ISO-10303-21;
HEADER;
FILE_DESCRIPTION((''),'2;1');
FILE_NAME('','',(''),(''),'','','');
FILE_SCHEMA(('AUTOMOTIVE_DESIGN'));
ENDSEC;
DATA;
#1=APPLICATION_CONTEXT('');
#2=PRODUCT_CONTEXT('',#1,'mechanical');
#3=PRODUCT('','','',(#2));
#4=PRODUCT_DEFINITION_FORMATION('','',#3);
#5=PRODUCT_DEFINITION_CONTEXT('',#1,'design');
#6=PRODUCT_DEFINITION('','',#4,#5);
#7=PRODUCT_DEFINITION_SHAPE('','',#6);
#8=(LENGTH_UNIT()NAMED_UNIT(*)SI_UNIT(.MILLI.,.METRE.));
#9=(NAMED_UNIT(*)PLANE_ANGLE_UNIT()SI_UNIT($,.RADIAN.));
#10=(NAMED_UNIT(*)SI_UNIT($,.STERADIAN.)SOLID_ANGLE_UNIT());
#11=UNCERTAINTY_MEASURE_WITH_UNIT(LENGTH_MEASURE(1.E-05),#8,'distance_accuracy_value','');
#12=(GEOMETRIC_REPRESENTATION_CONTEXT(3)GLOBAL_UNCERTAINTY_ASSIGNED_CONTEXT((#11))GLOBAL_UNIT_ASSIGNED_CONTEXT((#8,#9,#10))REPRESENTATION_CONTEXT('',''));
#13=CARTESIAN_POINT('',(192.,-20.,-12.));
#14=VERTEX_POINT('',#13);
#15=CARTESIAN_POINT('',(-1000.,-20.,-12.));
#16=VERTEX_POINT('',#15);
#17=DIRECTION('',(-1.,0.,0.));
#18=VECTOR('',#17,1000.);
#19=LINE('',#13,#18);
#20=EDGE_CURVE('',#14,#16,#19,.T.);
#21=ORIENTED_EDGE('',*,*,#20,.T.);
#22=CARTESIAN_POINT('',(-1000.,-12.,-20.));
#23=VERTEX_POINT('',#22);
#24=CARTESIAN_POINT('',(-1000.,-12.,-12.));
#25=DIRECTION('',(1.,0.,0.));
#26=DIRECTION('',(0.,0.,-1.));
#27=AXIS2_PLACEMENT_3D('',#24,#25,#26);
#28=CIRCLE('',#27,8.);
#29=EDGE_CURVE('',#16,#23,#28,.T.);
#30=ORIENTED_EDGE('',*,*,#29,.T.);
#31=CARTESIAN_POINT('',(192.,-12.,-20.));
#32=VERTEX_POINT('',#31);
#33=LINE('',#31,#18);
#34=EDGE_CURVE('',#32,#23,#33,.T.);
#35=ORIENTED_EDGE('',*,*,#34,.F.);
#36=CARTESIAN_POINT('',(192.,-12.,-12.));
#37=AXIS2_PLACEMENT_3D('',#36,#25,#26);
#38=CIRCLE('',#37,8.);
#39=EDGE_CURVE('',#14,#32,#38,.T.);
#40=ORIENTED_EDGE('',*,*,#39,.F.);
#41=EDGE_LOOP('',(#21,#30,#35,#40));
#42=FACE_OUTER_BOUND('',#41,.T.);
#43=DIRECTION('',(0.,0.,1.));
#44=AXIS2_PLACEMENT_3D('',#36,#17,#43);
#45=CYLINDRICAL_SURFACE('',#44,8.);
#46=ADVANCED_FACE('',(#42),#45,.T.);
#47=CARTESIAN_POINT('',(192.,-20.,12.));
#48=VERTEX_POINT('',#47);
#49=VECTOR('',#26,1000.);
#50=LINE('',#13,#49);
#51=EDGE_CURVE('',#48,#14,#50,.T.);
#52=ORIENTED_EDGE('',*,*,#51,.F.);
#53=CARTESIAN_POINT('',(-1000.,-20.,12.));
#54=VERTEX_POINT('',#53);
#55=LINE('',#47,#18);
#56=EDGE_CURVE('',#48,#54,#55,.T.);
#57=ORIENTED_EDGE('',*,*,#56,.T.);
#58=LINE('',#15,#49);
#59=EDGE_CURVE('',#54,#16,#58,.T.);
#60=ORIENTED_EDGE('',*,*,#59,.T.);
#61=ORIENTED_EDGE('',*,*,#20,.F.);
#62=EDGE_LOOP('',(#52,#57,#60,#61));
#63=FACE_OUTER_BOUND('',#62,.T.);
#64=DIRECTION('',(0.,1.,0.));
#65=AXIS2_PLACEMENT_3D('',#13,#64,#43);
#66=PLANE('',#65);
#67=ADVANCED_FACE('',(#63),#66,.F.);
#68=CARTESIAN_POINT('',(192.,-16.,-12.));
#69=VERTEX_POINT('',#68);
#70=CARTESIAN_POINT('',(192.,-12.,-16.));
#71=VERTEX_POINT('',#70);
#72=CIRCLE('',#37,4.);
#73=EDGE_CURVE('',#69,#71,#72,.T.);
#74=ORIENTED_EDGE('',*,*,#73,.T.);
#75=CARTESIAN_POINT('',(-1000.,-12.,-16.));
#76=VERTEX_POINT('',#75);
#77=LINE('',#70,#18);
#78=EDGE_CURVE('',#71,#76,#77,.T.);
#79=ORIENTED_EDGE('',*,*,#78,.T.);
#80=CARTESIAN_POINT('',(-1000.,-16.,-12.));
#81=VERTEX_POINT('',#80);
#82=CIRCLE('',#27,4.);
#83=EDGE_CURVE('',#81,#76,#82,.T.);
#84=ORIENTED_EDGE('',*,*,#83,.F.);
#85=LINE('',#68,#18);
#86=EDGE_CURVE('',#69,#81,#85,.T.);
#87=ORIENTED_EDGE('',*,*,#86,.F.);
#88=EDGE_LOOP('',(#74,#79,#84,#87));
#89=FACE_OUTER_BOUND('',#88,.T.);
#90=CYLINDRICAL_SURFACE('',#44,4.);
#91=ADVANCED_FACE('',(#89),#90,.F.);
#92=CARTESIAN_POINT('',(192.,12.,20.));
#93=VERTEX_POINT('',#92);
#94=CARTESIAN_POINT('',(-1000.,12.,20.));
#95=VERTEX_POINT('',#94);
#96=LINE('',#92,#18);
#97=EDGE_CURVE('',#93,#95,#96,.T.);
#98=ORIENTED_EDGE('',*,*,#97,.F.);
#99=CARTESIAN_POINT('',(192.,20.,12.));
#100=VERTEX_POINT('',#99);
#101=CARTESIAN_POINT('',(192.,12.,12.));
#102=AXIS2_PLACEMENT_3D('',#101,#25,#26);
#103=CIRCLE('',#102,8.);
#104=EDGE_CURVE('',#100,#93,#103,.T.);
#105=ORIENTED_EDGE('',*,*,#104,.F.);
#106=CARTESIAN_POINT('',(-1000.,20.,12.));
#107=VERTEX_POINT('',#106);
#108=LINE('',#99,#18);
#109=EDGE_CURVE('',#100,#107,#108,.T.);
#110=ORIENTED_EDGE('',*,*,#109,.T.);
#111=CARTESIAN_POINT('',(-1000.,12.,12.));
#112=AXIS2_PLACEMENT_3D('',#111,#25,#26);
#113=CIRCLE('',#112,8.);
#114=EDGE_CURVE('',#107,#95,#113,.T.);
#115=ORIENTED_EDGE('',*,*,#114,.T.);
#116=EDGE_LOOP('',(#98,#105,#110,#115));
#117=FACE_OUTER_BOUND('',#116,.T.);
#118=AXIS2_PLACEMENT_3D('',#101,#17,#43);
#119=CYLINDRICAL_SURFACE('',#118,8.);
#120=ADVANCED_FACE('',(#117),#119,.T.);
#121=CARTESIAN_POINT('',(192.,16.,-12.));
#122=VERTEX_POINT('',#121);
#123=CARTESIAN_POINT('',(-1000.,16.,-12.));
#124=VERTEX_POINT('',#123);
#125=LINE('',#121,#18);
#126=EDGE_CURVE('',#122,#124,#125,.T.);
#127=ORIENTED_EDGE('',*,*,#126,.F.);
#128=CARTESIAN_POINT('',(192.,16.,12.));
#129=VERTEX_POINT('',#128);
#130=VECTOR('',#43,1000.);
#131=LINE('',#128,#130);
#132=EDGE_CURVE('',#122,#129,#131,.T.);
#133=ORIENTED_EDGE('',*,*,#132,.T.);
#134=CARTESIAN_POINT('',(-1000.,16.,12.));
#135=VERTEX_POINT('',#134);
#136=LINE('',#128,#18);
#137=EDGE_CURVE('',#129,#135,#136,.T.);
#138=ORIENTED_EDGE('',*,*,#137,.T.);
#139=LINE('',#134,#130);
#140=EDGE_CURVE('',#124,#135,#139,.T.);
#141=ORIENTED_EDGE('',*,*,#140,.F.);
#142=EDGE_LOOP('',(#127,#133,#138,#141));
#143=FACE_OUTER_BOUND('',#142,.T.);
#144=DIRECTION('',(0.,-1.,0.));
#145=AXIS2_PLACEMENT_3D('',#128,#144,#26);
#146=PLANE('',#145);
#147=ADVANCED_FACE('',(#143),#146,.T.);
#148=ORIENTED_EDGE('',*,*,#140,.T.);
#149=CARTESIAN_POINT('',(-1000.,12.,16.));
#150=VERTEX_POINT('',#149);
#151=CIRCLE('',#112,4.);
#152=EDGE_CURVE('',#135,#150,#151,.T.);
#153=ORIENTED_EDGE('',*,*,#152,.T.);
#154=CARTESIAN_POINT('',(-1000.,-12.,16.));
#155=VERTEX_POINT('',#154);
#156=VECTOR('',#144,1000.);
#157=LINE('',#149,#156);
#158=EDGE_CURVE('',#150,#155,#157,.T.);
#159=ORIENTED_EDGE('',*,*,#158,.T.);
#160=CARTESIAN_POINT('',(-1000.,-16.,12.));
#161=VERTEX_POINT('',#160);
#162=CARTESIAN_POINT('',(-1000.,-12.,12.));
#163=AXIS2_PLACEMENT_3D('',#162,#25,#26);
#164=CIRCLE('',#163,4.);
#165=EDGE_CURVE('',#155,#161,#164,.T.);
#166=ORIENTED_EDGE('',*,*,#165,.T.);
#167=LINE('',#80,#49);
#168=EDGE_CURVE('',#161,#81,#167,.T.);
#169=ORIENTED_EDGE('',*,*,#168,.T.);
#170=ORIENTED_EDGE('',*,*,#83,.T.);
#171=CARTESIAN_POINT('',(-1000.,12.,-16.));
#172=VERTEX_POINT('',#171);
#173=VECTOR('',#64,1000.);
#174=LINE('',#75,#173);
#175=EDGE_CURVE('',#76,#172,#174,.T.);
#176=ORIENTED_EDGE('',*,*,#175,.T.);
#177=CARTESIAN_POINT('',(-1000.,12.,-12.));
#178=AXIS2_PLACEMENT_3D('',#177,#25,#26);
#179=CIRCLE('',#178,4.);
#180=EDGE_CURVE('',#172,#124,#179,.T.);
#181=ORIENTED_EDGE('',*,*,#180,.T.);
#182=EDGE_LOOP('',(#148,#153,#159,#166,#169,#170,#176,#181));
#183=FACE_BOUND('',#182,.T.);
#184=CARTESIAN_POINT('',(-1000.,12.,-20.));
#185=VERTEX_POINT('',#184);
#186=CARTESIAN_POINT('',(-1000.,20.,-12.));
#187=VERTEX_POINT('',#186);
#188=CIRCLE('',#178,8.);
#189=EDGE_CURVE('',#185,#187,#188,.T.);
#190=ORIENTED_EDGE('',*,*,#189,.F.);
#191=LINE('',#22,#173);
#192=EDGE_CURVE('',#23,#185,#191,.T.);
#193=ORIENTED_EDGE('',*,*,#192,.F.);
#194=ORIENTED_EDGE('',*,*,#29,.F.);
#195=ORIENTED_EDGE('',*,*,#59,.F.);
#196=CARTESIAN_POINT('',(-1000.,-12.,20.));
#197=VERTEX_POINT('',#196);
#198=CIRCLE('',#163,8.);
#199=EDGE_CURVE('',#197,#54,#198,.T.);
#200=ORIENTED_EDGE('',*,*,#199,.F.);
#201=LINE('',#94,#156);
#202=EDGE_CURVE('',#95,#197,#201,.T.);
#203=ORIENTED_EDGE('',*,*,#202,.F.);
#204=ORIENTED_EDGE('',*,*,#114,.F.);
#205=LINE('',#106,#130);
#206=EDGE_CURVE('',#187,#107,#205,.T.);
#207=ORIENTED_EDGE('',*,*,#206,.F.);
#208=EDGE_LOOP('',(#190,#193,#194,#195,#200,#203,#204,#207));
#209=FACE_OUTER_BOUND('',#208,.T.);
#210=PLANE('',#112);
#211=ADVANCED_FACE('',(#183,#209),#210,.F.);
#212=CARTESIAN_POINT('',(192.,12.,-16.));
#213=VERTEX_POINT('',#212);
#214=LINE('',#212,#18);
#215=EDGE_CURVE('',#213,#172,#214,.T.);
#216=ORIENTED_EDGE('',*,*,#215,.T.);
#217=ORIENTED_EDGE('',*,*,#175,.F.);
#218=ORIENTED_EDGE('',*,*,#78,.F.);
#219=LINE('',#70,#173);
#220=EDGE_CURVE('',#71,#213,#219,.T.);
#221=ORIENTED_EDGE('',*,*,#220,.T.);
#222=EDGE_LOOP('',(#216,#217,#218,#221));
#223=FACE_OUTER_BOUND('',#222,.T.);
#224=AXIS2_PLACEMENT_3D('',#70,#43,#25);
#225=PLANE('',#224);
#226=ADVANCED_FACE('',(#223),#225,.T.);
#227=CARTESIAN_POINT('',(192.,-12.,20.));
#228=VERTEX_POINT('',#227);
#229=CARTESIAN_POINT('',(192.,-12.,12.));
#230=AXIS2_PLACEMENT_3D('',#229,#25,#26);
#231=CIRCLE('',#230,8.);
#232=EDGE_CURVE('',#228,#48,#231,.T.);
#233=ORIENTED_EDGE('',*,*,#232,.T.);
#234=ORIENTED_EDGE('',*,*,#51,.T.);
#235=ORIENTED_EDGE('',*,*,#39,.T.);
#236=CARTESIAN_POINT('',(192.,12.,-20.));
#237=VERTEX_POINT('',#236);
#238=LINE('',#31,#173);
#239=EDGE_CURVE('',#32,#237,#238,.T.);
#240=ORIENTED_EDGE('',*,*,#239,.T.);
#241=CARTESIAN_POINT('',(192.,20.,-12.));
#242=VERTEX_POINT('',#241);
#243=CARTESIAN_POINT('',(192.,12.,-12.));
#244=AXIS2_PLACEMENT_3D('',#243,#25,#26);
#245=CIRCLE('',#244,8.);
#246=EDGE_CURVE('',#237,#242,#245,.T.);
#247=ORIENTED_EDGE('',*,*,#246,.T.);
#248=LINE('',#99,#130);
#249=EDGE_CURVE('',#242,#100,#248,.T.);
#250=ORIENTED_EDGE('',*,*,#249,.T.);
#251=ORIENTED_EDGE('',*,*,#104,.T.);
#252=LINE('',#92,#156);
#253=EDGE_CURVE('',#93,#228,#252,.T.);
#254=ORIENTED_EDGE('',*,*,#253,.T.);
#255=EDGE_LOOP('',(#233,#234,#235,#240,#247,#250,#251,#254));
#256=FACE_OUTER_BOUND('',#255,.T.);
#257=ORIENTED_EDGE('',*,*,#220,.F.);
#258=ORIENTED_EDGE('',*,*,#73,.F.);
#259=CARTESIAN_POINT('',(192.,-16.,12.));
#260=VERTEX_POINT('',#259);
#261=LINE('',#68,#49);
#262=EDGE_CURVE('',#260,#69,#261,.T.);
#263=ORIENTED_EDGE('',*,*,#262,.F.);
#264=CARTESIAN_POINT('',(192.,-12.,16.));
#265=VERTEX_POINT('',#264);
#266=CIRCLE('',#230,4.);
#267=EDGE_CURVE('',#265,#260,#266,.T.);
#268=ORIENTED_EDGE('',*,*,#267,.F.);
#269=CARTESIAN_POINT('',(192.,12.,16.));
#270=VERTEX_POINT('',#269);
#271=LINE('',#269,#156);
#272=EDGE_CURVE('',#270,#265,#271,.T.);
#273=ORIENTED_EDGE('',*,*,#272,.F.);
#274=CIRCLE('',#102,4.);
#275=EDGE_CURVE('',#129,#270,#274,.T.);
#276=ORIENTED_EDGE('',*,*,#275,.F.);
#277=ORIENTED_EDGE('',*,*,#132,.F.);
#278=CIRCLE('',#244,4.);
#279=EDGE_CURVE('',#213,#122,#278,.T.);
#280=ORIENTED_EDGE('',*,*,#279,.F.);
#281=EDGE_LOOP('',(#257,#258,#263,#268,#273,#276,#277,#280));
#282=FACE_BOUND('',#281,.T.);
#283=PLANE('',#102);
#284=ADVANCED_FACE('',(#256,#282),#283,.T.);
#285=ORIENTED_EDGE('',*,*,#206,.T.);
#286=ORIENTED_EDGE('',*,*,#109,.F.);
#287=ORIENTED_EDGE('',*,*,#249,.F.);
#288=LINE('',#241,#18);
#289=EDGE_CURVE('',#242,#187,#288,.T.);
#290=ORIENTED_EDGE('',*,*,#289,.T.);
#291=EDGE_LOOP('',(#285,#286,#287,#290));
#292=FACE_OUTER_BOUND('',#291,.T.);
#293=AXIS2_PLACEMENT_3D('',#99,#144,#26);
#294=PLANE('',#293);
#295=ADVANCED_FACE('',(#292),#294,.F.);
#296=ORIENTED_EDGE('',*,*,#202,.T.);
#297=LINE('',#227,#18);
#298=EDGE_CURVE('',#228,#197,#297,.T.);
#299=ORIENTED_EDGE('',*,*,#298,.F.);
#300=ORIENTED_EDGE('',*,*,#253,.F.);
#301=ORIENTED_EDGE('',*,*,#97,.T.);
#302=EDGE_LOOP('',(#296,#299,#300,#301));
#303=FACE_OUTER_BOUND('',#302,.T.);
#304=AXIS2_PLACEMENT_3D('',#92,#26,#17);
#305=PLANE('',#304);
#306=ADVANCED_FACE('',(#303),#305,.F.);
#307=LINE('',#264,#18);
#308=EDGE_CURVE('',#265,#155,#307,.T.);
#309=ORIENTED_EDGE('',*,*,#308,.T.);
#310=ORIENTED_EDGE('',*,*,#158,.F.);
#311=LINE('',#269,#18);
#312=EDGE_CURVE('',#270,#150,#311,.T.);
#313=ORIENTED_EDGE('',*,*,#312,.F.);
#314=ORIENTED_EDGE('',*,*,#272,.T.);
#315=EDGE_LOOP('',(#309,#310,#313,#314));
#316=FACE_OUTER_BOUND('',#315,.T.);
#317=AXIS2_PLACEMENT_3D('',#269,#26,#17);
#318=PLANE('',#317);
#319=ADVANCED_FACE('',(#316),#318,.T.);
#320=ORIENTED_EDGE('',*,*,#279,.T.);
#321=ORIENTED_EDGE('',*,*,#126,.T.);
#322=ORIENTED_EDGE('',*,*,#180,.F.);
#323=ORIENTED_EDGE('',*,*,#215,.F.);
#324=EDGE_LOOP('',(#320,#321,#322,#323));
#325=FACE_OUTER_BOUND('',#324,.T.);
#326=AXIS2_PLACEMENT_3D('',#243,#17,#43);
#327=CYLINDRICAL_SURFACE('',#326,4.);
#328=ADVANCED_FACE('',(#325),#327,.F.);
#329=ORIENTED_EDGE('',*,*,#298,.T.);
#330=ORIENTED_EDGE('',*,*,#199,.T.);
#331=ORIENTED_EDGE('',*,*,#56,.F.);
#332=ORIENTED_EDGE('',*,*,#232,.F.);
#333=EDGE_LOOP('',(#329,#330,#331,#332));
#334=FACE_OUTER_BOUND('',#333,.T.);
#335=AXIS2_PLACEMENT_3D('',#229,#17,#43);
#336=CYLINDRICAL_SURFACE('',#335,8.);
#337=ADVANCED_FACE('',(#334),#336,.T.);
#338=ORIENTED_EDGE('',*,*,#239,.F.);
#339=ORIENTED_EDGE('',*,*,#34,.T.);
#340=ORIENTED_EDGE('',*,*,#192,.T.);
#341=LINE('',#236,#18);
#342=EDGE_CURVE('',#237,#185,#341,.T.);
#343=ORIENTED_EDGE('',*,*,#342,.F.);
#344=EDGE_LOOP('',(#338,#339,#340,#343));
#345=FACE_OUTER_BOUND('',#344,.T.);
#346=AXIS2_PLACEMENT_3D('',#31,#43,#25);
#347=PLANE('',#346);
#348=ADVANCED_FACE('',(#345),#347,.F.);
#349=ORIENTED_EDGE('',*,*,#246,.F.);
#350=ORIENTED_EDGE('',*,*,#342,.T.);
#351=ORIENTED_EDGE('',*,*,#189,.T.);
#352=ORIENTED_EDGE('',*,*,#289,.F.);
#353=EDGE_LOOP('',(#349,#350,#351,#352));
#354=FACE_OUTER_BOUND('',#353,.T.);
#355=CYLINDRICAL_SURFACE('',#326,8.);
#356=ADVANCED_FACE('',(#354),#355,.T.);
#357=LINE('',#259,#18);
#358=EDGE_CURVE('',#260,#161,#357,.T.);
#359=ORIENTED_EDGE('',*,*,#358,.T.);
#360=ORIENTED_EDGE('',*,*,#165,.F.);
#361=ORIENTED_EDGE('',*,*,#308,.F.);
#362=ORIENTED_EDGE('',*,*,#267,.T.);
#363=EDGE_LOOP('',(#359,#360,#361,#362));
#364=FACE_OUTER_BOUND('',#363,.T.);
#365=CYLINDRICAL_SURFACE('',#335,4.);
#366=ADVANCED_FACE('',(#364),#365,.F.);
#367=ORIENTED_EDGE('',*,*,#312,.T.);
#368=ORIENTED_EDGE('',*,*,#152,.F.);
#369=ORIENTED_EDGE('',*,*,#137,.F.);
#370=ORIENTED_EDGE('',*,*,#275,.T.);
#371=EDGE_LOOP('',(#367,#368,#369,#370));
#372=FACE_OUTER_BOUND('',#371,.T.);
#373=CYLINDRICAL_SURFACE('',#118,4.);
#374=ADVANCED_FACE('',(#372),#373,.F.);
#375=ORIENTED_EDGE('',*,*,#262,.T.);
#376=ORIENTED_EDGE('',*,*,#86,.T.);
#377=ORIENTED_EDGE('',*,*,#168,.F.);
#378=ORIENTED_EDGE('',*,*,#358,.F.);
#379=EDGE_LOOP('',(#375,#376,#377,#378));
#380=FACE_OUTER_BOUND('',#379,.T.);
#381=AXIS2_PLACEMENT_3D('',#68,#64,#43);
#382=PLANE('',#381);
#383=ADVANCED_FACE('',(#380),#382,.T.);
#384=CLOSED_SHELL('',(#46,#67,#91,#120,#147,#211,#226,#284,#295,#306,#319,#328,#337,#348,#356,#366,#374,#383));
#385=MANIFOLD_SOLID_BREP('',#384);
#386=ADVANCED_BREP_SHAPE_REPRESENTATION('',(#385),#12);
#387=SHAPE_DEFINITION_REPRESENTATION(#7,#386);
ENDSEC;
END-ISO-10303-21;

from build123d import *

# Parameters (mm, degrees)
SQUARE_TUBE_40_X_40_X_4_1_DEPTH = 1192


with BuildPart() as part:
    # Sketch1 → Square Tube 40 X 40 X 4(1) (new body)
    with BuildSketch(Plane.YZ.offset(-1000)):
        with BuildLine():
            Line((-12, -20), (12, -20))
            ThreePointArc((12, -20), (17.656854249, -17.656854249), (20, -12))
            Line((20, -12), (20, 12))
            ThreePointArc((20, 12), (17.656854249, 17.656854249), (12, 20))
            Line((12, 20), (-12, 20))
            ThreePointArc((-12, 20), (-17.656854249, 17.656854249), (-20, 12))
            Line((-20, 12), (-20, -12))
            ThreePointArc((-20, -12), (-17.656854249, -17.656854249), (-12, -20))
        make_face()
        with BuildLine():
            Line((-12, -16), (12, -16))
            ThreePointArc((12, -16), (14.828427125, -14.828427125), (16, -12))
            Line((16, -12), (16, 12))
            ThreePointArc((16, 12), (14.828427125, 14.828427125), (12, 16))
            Line((12, 16), (-12, 16))
            ThreePointArc((-12, 16), (-14.828427125, 14.828427125), (-16, 12))
            Line((-16, 12), (-16, -12))
            ThreePointArc((-16, -12), (-14.828427125, -14.828427125), (-12, -16))
        make_face(mode=Mode.SUBTRACT)
    extrude(amount=SQUARE_TUBE_40_X_40_X_4_1_DEPTH)


solid = part.part
